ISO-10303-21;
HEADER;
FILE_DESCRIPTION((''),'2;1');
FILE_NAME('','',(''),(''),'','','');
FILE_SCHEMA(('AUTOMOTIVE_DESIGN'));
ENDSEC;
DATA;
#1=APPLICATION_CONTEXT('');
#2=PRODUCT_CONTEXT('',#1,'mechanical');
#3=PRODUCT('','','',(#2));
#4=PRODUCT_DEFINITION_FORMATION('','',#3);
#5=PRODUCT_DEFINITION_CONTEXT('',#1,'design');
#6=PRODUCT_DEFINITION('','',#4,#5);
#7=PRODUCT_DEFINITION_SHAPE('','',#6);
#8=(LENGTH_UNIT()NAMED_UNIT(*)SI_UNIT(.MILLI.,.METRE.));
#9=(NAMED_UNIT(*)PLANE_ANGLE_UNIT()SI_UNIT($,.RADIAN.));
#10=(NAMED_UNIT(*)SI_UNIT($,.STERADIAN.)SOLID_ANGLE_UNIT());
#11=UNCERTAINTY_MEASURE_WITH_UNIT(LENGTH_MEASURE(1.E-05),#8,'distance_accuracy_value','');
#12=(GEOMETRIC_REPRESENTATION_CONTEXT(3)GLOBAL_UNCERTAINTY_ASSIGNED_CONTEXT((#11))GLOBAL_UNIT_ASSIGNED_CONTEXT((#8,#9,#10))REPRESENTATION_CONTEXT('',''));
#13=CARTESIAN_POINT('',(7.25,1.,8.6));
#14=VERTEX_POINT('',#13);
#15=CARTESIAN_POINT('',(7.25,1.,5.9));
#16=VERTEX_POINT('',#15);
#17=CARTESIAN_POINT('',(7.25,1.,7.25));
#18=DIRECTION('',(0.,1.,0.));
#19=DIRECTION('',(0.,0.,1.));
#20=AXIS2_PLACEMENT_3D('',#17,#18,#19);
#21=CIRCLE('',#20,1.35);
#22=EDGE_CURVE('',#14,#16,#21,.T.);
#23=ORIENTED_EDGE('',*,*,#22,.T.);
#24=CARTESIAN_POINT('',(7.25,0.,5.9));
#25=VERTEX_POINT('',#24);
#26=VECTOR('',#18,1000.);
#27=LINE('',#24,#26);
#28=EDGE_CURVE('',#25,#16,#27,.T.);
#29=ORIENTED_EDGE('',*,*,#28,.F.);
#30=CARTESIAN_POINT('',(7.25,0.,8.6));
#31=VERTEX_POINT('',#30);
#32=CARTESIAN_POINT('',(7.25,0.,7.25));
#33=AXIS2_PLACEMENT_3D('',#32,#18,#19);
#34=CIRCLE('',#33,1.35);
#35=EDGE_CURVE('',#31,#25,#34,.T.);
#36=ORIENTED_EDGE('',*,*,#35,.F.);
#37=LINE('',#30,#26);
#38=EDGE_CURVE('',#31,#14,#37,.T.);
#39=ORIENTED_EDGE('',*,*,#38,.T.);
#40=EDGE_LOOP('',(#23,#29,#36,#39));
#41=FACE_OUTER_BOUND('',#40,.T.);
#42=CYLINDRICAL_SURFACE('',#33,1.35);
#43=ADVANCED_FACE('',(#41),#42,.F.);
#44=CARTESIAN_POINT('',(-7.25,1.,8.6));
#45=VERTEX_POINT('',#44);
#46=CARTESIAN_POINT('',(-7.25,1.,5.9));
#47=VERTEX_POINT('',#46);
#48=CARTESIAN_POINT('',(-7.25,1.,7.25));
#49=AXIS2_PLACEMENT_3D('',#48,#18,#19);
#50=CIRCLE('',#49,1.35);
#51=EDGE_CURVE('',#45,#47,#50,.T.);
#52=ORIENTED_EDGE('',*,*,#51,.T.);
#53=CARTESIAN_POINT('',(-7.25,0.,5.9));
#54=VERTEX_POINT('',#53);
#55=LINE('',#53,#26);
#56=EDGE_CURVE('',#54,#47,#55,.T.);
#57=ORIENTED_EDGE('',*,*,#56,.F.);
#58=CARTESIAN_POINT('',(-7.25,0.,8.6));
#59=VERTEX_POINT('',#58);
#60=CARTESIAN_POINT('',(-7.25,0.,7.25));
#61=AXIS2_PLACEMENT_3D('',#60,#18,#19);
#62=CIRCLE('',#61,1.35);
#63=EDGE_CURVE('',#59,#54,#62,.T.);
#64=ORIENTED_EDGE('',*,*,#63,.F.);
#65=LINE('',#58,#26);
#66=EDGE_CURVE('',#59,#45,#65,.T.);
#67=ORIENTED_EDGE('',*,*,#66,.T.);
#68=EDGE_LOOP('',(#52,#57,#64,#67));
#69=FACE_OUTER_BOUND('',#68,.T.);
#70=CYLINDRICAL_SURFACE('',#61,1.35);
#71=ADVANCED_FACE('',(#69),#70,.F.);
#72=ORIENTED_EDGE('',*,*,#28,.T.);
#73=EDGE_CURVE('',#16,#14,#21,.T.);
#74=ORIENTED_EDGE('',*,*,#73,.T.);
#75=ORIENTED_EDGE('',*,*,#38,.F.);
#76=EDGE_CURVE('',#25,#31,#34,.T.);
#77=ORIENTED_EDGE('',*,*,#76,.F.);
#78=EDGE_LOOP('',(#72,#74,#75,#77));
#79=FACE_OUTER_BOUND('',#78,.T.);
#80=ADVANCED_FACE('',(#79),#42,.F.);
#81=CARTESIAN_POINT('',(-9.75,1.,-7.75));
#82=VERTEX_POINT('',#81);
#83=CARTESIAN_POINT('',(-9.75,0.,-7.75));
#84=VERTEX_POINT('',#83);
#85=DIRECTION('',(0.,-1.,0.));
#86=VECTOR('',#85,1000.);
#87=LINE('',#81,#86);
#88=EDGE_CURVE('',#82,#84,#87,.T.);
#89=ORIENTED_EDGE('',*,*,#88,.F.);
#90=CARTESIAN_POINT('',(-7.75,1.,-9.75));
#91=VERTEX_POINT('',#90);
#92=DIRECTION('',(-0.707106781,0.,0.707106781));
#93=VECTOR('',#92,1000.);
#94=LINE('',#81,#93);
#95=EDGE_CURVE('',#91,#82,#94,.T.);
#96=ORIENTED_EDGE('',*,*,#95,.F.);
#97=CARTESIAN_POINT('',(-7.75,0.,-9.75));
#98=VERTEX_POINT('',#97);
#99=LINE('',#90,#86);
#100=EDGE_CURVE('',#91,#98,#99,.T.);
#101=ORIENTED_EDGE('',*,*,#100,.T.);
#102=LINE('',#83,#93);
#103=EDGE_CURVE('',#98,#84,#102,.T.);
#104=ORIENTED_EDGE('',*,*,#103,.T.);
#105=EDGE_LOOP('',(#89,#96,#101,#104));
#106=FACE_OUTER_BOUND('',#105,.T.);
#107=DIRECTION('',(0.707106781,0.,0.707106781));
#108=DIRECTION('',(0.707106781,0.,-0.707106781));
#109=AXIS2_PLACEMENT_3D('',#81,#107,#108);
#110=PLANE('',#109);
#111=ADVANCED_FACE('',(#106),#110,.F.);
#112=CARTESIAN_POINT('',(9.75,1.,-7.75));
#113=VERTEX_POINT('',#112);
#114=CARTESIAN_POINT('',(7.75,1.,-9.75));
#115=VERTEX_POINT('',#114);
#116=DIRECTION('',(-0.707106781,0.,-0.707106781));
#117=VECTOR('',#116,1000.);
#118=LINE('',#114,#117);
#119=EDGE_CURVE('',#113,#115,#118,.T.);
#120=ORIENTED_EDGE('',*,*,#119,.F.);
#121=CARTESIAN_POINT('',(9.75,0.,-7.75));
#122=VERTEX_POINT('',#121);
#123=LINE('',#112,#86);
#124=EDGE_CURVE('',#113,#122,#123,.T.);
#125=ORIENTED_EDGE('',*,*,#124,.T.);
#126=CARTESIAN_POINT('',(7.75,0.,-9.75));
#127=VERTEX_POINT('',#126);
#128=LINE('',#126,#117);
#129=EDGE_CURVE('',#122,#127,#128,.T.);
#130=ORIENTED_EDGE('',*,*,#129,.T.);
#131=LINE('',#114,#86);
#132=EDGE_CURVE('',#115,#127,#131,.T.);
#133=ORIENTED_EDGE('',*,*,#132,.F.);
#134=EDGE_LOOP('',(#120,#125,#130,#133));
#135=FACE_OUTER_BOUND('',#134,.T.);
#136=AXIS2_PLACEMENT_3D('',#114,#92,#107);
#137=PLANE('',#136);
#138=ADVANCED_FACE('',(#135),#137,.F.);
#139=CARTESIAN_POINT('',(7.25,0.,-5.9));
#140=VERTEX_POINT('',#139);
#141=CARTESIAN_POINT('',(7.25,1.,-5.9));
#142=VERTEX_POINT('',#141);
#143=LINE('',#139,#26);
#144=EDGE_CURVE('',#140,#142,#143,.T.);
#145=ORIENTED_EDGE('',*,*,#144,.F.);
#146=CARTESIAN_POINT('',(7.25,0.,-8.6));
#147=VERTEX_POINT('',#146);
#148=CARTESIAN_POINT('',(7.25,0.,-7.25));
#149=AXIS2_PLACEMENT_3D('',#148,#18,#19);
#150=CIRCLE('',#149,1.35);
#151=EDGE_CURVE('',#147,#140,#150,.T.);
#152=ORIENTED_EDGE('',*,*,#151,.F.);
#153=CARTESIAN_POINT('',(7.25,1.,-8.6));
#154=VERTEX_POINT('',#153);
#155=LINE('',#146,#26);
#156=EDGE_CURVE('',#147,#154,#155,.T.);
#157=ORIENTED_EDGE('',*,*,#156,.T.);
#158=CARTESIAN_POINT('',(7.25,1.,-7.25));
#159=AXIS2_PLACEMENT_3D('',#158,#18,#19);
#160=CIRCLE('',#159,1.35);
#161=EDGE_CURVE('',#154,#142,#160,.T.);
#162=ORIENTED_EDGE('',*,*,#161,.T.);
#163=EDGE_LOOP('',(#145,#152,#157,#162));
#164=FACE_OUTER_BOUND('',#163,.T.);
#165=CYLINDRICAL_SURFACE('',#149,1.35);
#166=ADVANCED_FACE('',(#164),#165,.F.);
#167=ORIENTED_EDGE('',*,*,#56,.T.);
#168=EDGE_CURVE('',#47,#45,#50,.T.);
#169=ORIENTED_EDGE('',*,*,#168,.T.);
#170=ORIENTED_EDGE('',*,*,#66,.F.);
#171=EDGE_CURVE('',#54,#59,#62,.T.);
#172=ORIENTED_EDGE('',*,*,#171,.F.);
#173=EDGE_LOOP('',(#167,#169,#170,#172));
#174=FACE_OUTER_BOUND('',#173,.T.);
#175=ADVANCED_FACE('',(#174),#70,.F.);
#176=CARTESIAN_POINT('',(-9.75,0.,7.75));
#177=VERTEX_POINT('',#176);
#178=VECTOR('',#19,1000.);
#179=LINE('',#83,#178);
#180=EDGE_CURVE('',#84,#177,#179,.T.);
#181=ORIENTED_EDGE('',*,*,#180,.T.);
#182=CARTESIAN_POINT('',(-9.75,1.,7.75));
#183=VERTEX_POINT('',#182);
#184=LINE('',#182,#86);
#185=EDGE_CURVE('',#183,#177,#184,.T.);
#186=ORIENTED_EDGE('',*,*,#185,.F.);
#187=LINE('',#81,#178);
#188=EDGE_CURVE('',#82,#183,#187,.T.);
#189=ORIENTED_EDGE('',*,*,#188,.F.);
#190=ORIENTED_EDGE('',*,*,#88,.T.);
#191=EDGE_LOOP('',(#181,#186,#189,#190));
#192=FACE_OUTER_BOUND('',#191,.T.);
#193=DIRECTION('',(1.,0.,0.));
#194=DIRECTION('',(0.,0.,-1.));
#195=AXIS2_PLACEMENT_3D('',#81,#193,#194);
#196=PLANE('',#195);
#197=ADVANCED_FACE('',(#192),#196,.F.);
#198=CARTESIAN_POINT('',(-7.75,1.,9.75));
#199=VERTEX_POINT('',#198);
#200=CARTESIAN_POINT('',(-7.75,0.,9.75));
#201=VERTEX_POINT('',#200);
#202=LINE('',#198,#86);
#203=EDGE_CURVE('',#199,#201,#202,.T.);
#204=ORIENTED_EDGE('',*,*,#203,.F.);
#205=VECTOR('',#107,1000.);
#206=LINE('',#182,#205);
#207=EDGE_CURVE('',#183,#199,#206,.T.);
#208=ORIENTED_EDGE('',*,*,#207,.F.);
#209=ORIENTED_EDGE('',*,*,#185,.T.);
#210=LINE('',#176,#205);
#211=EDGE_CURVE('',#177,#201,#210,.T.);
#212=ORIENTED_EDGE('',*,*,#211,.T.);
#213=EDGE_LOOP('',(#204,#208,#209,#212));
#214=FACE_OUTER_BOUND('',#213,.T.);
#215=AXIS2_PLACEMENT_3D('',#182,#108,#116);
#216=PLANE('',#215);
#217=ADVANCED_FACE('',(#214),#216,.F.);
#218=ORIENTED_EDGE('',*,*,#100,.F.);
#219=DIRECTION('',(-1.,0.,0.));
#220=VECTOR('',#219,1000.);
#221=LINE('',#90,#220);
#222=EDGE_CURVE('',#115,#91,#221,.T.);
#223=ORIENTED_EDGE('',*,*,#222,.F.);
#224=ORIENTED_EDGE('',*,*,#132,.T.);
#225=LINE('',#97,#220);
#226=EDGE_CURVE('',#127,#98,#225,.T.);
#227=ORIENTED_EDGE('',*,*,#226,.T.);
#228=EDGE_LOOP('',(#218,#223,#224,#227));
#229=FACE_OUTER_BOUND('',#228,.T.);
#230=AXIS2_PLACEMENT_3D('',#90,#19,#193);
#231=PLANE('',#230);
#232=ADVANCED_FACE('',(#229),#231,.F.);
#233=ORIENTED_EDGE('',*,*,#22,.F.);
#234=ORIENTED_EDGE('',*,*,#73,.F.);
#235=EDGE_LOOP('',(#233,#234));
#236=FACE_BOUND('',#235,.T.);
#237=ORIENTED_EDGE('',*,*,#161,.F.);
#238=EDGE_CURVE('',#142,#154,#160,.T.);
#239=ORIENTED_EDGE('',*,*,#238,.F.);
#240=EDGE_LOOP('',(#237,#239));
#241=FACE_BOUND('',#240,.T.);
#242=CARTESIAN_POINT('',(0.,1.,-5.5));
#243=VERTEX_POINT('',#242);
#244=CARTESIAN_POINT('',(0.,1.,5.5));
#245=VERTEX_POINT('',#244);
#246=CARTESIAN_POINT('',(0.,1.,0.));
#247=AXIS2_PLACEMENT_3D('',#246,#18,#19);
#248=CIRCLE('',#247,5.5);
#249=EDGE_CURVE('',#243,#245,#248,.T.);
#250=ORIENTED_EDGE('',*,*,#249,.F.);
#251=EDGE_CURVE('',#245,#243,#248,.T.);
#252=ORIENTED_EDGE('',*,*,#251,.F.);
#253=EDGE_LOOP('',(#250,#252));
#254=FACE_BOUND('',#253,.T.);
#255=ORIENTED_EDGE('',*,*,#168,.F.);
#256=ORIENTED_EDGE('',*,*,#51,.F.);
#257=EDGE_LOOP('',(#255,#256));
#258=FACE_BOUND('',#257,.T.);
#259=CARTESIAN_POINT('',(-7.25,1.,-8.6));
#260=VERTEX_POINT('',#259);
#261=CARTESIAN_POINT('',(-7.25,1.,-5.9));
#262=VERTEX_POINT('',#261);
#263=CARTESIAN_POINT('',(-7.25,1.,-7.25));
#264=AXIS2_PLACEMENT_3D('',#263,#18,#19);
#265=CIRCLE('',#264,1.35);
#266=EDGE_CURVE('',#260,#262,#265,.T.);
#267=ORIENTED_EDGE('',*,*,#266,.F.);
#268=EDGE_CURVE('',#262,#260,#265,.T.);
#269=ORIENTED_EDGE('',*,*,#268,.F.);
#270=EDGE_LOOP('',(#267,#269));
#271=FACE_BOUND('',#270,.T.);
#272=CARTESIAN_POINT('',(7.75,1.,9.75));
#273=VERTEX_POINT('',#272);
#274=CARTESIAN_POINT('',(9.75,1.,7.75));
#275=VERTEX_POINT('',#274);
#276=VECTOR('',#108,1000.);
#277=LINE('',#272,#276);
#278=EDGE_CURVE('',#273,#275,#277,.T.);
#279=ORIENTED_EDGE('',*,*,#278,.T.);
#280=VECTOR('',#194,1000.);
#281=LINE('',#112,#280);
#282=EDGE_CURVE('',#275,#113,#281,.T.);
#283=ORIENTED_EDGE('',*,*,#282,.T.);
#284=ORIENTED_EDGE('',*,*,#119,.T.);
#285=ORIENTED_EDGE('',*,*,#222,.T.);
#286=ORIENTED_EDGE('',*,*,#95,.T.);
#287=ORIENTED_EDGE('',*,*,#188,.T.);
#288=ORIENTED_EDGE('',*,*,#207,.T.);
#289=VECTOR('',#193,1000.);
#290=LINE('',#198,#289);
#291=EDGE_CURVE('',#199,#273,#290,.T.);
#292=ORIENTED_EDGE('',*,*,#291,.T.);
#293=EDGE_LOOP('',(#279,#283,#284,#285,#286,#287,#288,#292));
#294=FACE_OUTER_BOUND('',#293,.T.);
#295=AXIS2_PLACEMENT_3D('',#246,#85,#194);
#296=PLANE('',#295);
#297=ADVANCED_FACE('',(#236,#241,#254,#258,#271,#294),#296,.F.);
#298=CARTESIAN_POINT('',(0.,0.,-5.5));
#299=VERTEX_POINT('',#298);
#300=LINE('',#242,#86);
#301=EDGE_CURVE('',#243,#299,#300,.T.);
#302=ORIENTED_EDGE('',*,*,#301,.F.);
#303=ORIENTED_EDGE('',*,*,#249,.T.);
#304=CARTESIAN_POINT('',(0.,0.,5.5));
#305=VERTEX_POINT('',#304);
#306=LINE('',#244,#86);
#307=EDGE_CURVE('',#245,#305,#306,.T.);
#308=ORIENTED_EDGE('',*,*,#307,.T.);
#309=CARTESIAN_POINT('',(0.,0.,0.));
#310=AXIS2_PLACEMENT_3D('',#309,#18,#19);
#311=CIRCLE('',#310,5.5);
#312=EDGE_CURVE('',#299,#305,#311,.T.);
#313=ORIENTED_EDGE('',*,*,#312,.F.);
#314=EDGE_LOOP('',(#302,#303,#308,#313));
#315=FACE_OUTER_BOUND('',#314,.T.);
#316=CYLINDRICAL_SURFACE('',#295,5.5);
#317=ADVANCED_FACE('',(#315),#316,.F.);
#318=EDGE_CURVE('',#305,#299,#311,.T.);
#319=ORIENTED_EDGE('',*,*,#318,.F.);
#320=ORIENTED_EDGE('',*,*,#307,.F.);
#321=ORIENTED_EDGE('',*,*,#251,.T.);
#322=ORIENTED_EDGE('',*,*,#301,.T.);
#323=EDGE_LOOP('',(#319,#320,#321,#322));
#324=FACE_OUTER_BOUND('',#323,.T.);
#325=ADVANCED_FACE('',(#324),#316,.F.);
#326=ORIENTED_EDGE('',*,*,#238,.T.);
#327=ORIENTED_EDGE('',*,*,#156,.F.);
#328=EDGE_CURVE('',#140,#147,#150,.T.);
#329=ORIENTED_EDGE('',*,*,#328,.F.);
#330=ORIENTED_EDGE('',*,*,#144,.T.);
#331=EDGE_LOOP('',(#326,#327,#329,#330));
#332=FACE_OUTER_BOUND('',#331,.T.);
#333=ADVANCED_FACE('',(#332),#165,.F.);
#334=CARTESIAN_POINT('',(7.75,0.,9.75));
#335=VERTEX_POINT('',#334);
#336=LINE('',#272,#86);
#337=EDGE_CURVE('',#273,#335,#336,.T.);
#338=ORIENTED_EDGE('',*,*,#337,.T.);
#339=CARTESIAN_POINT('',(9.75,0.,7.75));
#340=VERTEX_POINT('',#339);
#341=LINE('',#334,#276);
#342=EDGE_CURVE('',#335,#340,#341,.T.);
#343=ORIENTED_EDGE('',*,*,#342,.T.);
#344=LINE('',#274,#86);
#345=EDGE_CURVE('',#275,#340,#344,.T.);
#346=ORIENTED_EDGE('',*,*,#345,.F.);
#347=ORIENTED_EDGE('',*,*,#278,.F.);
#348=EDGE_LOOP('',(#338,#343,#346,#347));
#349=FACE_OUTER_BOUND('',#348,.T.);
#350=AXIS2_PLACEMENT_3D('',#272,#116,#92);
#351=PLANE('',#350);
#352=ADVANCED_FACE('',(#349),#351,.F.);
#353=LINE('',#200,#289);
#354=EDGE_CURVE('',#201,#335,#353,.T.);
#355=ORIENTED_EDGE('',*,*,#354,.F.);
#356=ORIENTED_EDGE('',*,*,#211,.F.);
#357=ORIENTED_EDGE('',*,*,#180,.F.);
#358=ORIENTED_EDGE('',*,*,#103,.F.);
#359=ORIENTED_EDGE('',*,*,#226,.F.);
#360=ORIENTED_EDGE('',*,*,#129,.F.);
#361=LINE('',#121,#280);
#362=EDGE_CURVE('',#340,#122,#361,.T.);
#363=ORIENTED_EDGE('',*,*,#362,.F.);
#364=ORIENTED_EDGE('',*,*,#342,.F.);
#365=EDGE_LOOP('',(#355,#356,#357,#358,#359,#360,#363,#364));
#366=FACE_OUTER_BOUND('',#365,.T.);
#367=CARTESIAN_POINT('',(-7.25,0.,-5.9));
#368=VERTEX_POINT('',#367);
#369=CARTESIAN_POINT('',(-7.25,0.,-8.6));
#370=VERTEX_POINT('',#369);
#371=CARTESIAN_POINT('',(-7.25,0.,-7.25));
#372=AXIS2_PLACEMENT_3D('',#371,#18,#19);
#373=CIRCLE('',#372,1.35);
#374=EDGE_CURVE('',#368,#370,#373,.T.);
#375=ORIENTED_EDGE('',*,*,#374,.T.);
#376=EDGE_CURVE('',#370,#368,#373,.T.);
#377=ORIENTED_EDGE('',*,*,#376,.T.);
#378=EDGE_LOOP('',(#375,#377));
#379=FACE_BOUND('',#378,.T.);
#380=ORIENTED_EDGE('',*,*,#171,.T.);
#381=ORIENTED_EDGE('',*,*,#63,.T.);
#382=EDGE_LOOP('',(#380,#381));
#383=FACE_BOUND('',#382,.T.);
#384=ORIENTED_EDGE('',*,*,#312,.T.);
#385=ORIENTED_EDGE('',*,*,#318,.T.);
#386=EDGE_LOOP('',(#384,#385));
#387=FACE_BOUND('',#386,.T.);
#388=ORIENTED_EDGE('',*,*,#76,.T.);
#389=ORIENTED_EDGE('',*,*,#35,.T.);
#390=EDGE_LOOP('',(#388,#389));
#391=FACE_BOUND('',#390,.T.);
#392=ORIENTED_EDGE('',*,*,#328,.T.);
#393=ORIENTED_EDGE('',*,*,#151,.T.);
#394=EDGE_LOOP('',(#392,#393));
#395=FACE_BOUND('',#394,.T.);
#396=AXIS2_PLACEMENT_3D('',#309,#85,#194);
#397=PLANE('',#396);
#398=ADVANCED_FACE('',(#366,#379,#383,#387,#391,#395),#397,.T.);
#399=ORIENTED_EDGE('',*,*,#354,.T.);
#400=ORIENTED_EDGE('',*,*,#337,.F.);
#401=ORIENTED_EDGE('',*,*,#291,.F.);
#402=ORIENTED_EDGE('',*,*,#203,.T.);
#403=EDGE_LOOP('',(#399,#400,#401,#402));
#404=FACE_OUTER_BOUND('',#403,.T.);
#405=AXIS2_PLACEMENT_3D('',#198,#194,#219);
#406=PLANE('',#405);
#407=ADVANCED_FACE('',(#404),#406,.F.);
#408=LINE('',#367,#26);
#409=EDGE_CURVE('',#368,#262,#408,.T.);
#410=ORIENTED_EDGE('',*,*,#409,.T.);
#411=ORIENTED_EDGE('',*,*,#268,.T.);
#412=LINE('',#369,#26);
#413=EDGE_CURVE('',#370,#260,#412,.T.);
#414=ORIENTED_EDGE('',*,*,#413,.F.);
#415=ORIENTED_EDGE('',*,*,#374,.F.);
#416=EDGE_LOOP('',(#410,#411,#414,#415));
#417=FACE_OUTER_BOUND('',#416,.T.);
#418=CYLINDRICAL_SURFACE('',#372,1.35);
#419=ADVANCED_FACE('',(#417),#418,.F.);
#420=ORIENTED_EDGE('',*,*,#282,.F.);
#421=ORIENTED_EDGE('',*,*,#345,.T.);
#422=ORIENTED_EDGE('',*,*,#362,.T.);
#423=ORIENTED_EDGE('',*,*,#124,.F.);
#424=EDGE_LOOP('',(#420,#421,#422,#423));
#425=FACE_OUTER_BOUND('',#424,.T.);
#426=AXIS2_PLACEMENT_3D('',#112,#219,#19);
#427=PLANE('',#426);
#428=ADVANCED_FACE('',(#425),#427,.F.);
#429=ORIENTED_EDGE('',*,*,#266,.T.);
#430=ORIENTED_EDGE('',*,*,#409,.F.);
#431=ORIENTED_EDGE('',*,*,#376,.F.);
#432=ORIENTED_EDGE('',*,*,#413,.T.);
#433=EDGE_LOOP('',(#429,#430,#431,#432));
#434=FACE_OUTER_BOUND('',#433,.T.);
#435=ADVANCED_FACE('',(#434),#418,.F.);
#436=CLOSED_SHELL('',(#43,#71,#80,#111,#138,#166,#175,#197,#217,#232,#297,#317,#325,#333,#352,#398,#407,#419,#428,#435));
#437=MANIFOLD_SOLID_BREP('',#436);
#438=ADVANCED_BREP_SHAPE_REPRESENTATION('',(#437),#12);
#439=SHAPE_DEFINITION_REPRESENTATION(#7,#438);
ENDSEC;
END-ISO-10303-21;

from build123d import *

# Parameters (mm, degrees)
SKETCH1_R           = 5.5
BOSS_EXTRUDE1_DEPTH = 1
SKETCH2_R           = 1.35
CUT_EXTRUDE1_DEPTH  = 1


with BuildPart() as part:
    # Sketch1 → Boss-Extrude1 (new body)
    with BuildSketch(Plane(origin=(0, 0, 0), x_dir=(1, 0, 0), z_dir=(0, 1, 0))):
        Polygon((7.75, -9.75), (9.75, -7.75), (9.75, 7.75), (7.75, 9.75), (-7.75, 9.75), (-9.75, 7.75), (-9.75, -7.75), (-7.75, -9.75), align=None)
        with Locations(Location((0, 0, 0), (0, 0, 270))):
            Circle(SKETCH1_R, mode=Mode.SUBTRACT)
    extrude(amount=BOSS_EXTRUDE1_DEPTH)

    # Sketch2 → Cut-Extrude1 (cut)
    with BuildSketch(Plane(origin=(0, 1, 0), x_dir=(1, 0, 0), z_dir=(0, 1, 0))):
        with Locations(Location((-7.25, 7.25, 0), (0, 0, 270))):
            Circle(SKETCH2_R)
        with Locations(Location((7.25, 7.25, 0), (0, 0, 270))):
            Circle(SKETCH2_R)
        with Locations(Location((7.25, -7.25, 0), (0, 0, 270))):
            Circle(SKETCH2_R)
        with Locations(Location((-7.25, -7.25, 0), (0, 0, 270))):
            Circle(SKETCH2_R)
    extrude(amount=-CUT_EXTRUDE1_DEPTH, mode=Mode.SUBTRACT)


solid = part.part
